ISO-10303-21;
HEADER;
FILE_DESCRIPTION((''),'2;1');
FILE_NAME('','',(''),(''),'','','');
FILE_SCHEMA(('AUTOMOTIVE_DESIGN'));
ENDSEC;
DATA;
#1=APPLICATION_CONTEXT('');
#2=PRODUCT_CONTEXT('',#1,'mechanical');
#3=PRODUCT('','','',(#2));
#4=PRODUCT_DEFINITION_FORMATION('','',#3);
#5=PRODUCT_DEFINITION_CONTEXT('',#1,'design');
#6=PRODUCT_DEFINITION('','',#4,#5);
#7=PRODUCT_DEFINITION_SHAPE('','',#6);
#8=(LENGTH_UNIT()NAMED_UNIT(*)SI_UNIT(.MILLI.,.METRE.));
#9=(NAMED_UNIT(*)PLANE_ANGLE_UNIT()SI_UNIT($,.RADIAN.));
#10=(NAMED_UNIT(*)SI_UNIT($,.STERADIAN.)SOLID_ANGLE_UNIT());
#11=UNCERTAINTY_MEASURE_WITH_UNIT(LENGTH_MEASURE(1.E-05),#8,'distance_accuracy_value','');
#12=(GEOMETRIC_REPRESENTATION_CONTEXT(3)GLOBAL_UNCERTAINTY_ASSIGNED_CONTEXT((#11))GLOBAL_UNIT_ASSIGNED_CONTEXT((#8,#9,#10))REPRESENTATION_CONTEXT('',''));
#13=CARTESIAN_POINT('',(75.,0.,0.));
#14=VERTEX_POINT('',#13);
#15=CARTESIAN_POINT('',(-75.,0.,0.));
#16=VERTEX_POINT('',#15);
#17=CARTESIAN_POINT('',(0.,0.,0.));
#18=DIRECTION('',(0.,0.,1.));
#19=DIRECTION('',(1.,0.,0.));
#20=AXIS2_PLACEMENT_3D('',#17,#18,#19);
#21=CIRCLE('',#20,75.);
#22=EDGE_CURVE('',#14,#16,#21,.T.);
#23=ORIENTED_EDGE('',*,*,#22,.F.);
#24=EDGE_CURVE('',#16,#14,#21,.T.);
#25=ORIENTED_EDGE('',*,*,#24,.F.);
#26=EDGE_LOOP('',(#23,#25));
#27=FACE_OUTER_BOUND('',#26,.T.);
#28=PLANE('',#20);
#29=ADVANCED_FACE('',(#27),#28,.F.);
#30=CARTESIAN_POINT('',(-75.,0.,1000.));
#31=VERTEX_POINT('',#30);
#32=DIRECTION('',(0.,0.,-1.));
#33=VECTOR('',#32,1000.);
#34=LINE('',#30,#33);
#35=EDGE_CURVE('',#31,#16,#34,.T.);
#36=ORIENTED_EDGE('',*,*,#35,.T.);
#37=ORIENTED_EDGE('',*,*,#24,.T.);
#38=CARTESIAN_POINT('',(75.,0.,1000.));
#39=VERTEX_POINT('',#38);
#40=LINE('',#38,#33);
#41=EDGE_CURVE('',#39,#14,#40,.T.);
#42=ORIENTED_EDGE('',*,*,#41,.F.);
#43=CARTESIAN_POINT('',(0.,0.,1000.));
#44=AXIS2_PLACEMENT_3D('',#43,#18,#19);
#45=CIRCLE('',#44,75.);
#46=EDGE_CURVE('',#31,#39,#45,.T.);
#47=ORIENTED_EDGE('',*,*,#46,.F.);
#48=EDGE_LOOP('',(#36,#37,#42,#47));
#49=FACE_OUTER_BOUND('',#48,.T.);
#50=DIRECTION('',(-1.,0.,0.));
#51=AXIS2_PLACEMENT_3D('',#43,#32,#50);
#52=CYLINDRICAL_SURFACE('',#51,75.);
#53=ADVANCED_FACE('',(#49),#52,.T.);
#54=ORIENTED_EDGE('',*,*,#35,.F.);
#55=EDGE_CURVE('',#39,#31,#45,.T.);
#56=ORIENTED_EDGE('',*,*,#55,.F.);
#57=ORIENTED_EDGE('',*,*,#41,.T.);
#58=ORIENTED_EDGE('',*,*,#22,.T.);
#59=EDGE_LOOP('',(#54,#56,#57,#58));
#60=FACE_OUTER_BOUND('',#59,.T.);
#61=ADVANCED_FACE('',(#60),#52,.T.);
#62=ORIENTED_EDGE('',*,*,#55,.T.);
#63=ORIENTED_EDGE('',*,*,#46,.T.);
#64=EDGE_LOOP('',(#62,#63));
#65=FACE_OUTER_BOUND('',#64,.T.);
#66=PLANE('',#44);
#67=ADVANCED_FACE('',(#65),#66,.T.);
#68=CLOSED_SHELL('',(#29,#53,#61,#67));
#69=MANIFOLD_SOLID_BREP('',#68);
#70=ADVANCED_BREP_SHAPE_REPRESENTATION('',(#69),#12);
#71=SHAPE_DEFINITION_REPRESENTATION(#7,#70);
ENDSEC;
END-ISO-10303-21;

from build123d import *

# Parameters (mm, degrees)
SKETCH1_R    = 75
LENGTH_DEPTH = 1000


with BuildPart() as part:
    # Sketch1 → Length (new body)
    with BuildSketch(Plane.XY):
        Circle(SKETCH1_R)
    extrude(amount=LENGTH_DEPTH)


solid = part.part
